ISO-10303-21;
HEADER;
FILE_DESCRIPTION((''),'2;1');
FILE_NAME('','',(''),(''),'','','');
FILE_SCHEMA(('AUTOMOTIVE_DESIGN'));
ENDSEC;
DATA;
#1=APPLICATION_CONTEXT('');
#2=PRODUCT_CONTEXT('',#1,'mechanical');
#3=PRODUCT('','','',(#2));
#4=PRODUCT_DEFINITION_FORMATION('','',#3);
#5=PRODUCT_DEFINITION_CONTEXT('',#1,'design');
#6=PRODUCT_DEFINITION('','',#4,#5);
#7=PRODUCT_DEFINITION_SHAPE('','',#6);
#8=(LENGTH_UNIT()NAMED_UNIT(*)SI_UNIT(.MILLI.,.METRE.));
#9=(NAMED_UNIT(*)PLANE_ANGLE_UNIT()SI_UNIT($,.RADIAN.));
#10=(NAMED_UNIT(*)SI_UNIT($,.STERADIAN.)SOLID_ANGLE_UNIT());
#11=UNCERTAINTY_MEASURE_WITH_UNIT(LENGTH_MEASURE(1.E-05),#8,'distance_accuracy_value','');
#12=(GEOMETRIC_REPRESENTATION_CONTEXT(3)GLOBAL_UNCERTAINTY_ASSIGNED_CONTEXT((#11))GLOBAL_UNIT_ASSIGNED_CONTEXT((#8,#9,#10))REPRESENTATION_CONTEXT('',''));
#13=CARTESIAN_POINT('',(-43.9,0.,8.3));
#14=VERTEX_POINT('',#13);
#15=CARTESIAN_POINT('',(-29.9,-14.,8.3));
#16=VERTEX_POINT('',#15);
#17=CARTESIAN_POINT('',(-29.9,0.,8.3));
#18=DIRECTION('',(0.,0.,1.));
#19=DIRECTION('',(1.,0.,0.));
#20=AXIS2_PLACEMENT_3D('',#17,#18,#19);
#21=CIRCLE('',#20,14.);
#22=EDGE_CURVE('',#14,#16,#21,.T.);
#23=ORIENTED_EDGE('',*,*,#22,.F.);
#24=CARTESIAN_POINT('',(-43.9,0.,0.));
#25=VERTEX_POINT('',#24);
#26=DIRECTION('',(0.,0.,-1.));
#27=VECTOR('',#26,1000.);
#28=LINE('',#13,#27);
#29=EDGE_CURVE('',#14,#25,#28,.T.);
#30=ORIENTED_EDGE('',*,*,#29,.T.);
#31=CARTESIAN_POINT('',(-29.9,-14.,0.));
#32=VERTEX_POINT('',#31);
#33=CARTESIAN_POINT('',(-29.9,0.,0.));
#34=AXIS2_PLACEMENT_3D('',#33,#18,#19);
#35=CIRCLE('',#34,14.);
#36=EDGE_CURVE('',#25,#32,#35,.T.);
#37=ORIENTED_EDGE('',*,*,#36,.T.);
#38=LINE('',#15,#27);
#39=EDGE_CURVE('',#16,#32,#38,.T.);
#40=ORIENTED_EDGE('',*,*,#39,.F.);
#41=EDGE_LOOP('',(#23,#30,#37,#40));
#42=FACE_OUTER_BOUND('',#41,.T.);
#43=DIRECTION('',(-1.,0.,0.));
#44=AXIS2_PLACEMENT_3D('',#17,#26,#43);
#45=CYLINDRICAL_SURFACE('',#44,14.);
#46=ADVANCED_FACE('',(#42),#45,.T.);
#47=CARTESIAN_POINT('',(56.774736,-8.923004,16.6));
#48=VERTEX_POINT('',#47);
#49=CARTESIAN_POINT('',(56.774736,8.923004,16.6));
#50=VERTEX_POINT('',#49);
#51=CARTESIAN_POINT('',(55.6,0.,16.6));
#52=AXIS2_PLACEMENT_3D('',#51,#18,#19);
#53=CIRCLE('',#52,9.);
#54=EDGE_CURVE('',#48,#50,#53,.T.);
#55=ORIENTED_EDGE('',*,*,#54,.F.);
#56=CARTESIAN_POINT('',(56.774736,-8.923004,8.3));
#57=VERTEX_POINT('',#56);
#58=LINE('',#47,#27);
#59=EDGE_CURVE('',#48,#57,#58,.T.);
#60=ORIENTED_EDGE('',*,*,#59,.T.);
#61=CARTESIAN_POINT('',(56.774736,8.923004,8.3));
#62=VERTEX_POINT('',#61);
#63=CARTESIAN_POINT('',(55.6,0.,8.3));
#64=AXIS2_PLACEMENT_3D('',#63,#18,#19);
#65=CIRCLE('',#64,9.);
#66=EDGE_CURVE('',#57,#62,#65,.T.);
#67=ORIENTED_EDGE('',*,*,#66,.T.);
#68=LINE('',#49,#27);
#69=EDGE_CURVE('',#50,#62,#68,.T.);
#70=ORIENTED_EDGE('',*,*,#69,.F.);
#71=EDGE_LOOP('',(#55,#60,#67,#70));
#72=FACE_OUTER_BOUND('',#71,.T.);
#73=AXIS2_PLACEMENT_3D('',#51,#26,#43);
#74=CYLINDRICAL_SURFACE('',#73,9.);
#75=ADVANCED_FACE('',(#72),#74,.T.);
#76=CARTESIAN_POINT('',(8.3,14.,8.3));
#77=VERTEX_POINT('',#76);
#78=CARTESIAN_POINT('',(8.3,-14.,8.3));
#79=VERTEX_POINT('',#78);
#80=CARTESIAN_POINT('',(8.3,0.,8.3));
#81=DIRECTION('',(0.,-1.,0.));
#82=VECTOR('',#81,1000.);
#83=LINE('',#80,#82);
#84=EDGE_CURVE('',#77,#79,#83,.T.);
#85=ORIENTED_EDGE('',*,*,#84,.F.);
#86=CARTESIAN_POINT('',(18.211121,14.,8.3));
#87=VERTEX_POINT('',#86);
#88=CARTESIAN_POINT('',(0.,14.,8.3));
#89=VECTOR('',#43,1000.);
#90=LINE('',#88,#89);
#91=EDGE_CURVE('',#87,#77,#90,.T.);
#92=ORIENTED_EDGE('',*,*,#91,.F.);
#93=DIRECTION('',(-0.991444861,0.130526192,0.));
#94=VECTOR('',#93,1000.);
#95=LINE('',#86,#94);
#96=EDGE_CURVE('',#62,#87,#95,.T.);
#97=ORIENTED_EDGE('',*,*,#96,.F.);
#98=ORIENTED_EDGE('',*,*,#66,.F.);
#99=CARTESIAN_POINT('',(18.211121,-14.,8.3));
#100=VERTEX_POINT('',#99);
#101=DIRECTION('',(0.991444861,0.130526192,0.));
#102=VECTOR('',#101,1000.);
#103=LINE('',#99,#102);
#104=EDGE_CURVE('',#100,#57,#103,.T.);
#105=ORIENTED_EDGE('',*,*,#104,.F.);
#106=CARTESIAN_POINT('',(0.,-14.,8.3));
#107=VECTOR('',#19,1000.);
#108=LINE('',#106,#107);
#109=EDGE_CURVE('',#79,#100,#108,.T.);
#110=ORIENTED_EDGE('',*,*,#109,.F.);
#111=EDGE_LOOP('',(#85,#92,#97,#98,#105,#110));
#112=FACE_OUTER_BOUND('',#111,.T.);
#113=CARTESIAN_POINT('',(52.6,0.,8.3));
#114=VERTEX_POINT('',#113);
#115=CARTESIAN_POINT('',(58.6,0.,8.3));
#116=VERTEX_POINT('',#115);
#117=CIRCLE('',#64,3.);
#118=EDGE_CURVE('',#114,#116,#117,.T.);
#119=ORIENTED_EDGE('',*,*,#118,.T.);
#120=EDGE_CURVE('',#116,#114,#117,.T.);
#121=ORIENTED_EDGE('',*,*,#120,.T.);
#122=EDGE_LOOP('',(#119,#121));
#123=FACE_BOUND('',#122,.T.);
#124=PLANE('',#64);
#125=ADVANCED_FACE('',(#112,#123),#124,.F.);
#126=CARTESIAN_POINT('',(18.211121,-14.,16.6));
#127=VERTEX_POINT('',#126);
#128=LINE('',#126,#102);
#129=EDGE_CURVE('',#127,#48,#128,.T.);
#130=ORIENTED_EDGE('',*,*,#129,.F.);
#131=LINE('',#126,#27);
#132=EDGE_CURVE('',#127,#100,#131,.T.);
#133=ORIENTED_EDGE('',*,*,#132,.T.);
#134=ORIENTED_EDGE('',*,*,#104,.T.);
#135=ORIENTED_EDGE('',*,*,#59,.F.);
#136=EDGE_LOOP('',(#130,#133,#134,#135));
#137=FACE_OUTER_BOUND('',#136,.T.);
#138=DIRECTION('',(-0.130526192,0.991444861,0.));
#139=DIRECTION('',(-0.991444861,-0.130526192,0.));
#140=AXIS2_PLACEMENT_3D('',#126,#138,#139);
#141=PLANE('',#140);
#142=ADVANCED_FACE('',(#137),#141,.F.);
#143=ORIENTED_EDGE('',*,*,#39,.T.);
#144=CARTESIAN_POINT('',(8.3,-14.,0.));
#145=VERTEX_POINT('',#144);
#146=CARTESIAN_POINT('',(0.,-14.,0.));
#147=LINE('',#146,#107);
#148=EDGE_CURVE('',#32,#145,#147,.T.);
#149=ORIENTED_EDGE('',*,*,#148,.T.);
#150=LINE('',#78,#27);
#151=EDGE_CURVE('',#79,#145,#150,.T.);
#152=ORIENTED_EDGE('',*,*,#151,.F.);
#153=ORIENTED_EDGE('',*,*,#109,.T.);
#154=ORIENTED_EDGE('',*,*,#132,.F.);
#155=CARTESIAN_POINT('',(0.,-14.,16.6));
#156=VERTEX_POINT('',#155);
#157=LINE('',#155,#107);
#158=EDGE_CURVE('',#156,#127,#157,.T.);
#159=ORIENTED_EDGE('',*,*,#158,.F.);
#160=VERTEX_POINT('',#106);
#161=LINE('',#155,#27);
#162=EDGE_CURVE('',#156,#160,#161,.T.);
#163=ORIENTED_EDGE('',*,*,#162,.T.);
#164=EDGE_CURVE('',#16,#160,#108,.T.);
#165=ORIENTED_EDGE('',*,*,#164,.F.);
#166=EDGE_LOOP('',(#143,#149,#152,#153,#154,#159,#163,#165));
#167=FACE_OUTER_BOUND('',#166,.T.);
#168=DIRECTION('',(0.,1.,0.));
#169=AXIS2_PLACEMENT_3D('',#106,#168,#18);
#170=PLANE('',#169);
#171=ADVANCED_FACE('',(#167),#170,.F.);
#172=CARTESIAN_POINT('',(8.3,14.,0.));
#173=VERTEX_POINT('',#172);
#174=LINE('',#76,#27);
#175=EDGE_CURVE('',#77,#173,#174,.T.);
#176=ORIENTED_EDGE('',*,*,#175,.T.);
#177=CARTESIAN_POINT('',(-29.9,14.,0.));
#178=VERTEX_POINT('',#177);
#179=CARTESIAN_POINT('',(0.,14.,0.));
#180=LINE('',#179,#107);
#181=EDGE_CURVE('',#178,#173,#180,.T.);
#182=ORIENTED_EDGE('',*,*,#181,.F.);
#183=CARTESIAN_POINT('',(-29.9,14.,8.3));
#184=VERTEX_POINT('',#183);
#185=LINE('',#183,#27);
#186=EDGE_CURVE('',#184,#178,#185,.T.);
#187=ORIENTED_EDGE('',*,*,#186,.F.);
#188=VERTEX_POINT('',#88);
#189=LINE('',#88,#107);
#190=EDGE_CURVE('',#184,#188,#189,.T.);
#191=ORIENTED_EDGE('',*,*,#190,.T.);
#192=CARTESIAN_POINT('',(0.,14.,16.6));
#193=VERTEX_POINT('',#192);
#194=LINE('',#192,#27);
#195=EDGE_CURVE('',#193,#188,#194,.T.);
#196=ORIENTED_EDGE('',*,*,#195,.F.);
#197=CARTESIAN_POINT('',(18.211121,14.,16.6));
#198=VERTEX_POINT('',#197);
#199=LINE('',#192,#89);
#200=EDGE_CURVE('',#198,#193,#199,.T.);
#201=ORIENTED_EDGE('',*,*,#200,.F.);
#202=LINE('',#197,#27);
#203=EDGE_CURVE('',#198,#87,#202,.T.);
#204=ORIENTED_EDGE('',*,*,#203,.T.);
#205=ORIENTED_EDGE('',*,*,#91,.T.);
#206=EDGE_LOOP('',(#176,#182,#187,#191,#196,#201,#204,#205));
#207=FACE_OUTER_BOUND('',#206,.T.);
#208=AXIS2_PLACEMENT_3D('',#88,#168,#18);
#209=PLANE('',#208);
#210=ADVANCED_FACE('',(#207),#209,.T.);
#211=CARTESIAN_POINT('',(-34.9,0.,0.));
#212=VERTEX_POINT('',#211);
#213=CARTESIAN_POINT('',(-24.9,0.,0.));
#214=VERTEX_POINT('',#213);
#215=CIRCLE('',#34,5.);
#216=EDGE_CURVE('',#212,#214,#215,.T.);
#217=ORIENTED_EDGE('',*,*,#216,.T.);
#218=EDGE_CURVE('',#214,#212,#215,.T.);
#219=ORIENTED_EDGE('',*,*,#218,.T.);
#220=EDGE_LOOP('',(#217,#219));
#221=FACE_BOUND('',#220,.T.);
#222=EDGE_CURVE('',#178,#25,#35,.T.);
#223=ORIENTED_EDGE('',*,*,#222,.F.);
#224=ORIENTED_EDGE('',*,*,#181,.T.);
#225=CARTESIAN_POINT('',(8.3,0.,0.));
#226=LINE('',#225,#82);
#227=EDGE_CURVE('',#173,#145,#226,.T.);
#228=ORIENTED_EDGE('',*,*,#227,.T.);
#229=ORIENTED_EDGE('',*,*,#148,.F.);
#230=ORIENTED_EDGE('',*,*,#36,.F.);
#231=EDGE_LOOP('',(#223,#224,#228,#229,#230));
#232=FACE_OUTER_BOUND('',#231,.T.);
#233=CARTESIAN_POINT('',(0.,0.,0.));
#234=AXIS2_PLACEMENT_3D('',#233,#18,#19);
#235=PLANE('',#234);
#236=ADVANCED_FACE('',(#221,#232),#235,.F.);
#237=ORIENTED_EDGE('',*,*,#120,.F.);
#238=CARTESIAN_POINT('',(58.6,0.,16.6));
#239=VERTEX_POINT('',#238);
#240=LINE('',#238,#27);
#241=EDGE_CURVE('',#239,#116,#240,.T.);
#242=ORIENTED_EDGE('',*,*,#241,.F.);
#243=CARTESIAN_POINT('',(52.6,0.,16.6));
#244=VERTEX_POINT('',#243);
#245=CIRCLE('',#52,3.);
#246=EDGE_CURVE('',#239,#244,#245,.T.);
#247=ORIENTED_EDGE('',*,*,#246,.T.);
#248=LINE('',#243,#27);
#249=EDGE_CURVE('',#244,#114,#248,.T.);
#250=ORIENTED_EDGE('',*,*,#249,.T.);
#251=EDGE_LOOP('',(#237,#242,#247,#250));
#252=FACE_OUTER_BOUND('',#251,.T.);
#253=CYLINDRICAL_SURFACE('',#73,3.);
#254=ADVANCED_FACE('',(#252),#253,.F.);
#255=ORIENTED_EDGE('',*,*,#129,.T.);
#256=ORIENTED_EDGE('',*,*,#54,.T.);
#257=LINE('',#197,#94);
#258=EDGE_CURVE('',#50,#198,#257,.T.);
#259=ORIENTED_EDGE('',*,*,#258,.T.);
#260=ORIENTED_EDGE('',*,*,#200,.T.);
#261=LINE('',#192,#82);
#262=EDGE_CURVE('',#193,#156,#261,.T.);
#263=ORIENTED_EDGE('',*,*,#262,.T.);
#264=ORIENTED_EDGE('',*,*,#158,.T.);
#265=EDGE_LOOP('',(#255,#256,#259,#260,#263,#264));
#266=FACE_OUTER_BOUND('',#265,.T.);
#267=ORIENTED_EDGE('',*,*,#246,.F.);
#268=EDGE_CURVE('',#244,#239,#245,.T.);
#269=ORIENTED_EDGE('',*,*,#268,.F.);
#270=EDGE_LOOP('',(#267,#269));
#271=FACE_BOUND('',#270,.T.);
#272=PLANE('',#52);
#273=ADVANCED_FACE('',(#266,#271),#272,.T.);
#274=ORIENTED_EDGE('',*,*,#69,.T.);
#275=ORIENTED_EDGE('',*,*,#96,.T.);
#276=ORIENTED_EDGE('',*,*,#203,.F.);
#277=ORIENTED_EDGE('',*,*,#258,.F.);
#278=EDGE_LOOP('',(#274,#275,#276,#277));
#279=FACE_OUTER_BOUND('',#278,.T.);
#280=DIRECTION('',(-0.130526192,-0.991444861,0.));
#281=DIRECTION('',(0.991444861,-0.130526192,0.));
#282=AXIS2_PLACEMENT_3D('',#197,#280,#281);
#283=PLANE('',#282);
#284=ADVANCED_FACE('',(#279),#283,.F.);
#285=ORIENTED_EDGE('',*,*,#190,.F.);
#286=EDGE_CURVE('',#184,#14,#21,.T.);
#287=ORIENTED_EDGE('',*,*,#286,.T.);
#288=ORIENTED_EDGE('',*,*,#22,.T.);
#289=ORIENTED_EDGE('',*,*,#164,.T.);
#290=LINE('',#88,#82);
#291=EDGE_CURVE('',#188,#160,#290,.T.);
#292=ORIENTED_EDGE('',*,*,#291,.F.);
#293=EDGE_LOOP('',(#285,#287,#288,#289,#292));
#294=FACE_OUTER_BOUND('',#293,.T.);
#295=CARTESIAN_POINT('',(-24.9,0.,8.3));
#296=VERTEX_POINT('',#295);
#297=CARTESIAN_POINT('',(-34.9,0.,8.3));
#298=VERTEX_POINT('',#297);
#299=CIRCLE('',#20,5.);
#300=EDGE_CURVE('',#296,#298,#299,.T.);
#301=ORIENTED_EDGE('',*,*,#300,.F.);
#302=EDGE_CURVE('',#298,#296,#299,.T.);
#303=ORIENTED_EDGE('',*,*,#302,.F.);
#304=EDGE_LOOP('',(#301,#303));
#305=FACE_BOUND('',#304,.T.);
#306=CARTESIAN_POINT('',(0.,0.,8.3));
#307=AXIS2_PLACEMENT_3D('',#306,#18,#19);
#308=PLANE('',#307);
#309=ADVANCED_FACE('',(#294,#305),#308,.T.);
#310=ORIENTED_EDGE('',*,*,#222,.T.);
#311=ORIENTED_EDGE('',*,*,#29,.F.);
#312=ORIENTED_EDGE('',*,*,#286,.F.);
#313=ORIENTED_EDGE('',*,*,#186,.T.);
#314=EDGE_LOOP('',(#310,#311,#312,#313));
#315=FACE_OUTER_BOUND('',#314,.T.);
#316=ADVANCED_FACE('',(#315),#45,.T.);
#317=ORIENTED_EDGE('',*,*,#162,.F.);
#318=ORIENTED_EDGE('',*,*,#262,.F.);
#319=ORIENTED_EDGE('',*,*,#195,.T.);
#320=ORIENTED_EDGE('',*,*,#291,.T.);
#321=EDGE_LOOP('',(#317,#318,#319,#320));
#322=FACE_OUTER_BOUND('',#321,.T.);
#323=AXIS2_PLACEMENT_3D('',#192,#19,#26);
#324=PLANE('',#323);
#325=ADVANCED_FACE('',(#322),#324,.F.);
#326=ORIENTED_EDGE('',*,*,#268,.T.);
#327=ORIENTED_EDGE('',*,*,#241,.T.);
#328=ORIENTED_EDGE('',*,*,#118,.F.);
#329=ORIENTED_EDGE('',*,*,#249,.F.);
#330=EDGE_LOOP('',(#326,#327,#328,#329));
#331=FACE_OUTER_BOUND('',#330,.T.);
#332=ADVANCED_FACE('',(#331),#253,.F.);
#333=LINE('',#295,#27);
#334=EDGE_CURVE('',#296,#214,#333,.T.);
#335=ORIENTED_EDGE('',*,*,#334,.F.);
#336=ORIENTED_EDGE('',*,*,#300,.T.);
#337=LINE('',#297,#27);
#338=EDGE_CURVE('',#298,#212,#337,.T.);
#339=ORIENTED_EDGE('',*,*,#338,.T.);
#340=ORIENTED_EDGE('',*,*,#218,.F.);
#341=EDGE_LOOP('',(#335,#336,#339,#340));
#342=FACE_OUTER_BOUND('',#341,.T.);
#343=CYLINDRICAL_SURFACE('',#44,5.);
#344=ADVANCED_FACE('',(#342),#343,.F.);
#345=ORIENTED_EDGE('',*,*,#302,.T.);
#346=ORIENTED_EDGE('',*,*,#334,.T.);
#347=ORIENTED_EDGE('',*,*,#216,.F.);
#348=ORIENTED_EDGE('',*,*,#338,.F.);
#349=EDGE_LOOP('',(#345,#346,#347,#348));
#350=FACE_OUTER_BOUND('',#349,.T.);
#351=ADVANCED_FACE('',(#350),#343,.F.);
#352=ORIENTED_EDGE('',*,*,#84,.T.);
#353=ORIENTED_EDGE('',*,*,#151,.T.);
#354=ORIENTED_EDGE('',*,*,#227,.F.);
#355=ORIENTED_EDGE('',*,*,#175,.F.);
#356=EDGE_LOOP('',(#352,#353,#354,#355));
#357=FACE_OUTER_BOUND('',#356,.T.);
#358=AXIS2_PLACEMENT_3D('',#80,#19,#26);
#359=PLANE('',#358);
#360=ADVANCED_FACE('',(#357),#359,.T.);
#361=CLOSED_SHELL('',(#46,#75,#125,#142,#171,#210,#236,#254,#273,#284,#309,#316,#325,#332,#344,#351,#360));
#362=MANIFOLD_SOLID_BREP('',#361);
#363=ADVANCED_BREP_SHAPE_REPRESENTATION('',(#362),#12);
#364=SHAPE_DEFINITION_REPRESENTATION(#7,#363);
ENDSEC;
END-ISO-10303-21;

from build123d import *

# Parameters (mm, degrees)
SKETCH1_R           = 5
SKETCH1_W           = 8.3
SKETCH1_H           = 28
BOSS_EXTRUDE2_DEPTH = 8.3
SKETCH2_R           = 3
BOSS_EXTRUDE4_DEPTH = 8.3


with BuildPart() as part:
    # Sketch1 → Boss-Extrude2 (new body)
    # profile 1 of 2: a face of its own
    with BuildSketch(Plane.XY):
        with BuildLine():
            Line((-29.9, 14), (0, 14))
            Line((0, 14), (0, -14))
            Line((0, -14), (-29.9, -14))
            ThreePointArc((-29.9, -14), (-43.9, 0), (-29.9, 14))
        make_face()
        with Locations(Location((-29.9, 0, 0), (0, 0, 180))):
            Circle(SKETCH1_R, mode=Mode.SUBTRACT)
    # profile 2 of 2: a face of its own
    with BuildSketch(Plane.XY):
        with Locations((4.15, 0)):
            Rectangle(SKETCH1_W, SKETCH1_H)
    extrude(amount=BOSS_EXTRUDE2_DEPTH)

    # Sketch2 → Boss-Extrude4 (add)
    with BuildSketch(Plane.XY.offset(8.3)):
        with BuildLine():
            Line((0, 14), (0, -14))
            Line((0, -14), (18.211120602, -14))
            Line((18.211120602, -14), (56.77473573, -8.923003752))
            ThreePointArc((56.77473573, -8.923003752), (64.6, 0), (56.77473573, 8.923003752))
            Line((56.77473573, 8.923003752), (18.211120602, 14))
            Line((18.211120602, 14), (0, 14))
        make_face()
        with Locations(Location((55.6, 0, 0), (0, 0, 180))):
            Circle(SKETCH2_R, mode=Mode.SUBTRACT)
    extrude(amount=BOSS_EXTRUDE4_DEPTH)


solid = part.part
